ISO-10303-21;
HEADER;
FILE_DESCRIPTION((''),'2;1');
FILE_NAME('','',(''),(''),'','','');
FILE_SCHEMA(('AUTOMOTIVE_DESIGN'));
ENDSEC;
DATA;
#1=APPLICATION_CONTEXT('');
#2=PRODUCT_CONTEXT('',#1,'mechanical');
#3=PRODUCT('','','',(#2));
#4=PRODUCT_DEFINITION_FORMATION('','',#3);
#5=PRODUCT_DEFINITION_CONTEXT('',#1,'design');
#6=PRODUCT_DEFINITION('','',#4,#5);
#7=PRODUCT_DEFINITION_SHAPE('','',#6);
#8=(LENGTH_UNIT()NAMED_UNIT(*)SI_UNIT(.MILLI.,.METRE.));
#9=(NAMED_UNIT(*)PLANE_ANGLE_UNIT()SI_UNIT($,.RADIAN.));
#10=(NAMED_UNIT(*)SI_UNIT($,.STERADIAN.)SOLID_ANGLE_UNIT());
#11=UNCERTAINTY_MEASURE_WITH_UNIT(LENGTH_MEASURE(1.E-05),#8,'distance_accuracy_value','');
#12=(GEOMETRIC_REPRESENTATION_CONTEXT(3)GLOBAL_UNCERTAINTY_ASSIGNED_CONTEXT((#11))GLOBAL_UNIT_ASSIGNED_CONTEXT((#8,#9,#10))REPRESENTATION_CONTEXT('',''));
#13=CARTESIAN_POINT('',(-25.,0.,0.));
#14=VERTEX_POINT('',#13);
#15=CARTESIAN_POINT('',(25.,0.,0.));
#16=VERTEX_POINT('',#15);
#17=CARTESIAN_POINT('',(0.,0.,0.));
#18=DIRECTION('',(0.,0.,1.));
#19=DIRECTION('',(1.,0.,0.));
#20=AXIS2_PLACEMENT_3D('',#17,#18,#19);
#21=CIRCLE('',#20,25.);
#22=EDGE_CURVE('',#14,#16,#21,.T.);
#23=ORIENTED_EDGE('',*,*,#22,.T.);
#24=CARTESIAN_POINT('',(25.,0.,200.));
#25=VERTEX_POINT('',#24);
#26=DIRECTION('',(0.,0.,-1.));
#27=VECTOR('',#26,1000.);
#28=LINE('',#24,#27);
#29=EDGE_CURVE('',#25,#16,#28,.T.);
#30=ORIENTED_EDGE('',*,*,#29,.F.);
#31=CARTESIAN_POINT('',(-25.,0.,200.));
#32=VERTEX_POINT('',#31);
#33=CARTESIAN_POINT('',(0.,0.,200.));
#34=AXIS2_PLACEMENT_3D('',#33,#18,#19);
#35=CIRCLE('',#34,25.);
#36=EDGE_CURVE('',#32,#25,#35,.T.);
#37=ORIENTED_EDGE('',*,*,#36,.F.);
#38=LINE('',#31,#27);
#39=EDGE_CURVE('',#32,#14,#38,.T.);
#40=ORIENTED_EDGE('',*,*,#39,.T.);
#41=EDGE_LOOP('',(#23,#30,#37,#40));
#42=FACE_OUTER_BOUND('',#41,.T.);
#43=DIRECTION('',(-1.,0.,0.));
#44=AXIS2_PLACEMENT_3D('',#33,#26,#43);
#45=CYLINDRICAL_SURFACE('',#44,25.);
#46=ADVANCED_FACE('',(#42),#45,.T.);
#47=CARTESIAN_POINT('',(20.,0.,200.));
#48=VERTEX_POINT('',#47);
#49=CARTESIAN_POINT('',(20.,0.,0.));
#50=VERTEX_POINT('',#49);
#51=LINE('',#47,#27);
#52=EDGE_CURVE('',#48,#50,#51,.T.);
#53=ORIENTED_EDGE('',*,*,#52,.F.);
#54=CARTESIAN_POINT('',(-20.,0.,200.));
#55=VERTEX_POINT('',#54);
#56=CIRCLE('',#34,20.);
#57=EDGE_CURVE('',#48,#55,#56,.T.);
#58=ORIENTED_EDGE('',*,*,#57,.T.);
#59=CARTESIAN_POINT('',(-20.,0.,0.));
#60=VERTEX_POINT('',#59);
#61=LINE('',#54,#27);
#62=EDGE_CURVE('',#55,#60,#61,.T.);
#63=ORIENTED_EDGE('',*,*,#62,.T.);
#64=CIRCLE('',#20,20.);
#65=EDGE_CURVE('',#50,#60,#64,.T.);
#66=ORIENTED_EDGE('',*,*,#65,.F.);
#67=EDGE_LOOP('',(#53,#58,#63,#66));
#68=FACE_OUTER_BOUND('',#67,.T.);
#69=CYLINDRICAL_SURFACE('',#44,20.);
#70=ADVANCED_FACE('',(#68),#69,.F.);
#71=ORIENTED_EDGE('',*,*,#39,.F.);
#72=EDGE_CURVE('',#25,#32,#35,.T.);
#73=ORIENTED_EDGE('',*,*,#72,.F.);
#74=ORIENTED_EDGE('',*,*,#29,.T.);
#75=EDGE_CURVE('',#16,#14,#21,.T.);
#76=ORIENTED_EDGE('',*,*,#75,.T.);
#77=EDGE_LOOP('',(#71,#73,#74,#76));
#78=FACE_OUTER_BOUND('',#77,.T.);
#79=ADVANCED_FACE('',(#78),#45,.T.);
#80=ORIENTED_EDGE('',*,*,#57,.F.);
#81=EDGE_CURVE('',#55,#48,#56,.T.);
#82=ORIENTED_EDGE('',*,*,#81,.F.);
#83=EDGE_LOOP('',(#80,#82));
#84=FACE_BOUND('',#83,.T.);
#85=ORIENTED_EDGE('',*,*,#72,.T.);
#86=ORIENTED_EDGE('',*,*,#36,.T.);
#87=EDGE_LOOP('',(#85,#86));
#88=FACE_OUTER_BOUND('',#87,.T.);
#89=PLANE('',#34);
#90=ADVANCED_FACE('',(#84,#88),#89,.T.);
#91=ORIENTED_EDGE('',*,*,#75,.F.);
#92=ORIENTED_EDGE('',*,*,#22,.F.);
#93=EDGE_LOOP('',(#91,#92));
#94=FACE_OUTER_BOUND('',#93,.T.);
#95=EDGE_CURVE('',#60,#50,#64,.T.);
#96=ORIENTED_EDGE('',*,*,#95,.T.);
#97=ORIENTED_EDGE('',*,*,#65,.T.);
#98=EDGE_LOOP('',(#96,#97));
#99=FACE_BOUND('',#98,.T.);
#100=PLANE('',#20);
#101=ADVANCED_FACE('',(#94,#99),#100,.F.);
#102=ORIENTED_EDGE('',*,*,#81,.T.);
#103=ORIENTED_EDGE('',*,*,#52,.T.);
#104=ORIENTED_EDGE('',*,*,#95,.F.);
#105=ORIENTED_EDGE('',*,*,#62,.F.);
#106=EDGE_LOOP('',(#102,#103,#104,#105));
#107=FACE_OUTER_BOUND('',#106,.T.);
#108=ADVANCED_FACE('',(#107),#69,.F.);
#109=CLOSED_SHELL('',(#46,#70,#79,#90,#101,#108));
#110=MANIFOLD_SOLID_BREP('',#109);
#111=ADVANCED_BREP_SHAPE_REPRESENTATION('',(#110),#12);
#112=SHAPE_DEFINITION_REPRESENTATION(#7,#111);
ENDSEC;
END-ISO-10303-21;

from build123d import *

# Parameters (mm, degrees)
SKETCH_1_R      = 25
SKETCH_1_R_2    = 20
EXTRUDE_1_DEPTH = 200


with BuildPart() as part:
    # 草图1 → 凸台-拉伸1 (new body)
    with BuildSketch(Plane.XY):
        Circle(SKETCH_1_R)
        Circle(SKETCH_1_R_2, mode=Mode.SUBTRACT)
    extrude(amount=EXTRUDE_1_DEPTH)


solid = part.part
